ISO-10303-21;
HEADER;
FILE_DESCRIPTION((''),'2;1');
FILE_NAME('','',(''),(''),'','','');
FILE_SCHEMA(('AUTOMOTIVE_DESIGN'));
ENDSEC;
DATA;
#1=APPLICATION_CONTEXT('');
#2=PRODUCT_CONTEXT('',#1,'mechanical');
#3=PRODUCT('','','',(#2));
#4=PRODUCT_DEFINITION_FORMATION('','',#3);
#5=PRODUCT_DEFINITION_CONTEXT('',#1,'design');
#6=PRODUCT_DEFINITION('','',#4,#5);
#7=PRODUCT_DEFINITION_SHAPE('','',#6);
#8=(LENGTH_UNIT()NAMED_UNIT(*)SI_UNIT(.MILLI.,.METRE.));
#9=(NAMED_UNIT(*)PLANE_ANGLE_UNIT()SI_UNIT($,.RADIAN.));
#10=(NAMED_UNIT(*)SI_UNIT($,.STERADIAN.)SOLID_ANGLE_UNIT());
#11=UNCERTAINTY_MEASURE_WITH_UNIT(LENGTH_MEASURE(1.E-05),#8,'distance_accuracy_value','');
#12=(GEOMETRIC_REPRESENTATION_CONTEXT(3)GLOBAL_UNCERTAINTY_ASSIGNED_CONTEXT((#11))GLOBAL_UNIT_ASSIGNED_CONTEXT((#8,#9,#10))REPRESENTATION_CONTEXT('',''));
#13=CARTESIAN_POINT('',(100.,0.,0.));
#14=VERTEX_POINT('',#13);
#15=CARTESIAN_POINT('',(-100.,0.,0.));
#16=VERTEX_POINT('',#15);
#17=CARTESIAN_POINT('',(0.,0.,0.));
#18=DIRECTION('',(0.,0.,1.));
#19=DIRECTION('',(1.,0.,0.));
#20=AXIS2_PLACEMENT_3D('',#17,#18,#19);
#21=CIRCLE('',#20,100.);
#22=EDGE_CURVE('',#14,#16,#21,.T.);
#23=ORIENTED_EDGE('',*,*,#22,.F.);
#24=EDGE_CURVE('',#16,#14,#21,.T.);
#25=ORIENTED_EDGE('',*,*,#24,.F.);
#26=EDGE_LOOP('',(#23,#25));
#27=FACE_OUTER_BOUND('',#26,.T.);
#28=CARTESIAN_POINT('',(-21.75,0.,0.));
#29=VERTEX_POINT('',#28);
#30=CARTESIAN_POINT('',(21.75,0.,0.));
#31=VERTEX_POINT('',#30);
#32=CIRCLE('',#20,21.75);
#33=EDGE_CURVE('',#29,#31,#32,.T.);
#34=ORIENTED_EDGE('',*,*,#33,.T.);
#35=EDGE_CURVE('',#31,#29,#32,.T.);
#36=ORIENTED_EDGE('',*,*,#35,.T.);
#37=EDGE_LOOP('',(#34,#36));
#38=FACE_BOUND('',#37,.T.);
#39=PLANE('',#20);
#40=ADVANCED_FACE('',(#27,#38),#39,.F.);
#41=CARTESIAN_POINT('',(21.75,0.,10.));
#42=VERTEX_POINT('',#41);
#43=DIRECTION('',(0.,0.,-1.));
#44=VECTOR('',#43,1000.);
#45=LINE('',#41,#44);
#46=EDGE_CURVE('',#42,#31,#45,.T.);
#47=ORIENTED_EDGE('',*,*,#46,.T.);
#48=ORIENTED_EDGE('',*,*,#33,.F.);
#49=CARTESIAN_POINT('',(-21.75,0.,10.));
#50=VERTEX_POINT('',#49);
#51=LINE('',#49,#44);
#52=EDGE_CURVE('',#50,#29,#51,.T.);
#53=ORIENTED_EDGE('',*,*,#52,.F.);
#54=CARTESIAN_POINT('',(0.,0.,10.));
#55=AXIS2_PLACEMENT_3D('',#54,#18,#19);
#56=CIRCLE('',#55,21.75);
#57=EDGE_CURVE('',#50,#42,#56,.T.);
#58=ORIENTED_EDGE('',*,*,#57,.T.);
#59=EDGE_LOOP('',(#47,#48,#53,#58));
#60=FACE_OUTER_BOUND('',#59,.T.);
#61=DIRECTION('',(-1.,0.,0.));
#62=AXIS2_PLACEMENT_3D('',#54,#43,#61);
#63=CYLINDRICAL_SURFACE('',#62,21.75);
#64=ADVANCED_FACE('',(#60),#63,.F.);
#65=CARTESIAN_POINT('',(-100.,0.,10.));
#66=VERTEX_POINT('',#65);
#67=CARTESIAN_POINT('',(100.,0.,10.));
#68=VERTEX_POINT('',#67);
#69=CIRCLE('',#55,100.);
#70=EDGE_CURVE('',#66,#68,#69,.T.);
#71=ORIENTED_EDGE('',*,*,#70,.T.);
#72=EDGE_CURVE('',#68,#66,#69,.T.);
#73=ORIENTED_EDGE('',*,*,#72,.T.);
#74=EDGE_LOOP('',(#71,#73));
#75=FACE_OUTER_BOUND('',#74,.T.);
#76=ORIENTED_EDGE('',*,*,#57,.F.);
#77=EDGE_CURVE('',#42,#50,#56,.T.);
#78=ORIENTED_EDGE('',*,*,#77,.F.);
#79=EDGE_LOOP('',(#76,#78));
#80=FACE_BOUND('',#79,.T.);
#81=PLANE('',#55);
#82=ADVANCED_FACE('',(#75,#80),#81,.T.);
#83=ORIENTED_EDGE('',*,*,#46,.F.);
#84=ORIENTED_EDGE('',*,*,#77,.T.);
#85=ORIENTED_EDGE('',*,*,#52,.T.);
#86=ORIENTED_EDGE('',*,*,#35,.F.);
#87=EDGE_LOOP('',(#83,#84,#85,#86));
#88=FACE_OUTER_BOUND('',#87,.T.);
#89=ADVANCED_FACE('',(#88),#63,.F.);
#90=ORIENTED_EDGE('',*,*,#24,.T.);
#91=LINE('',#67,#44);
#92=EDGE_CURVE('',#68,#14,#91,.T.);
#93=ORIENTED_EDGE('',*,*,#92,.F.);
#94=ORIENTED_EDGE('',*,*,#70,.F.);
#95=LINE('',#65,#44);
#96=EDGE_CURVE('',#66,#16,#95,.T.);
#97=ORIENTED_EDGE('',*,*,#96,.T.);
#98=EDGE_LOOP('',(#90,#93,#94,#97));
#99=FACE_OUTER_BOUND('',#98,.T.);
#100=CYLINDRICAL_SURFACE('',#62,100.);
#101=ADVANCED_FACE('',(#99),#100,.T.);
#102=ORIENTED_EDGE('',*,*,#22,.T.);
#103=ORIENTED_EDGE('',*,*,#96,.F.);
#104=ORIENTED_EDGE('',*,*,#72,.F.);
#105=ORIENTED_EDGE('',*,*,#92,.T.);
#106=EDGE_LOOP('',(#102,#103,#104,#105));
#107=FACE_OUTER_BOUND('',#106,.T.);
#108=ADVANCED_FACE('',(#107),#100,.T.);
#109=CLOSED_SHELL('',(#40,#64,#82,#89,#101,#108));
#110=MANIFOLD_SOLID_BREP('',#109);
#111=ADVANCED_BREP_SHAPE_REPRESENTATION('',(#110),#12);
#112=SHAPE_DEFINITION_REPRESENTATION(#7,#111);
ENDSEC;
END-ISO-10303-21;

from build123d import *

# Parameters (mm, degrees)
SKETCH_1_R      = 100
SKETCH_1_R_2    = 21.75
EXTRUDE_1_DEPTH = 10


with BuildPart() as part:
    # 草图1 → 凸台-拉伸1 (new body)
    with BuildSketch(Plane.XY):
        Circle(SKETCH_1_R)
        Circle(SKETCH_1_R_2, mode=Mode.SUBTRACT)
    extrude(amount=EXTRUDE_1_DEPTH)


solid = part.part
